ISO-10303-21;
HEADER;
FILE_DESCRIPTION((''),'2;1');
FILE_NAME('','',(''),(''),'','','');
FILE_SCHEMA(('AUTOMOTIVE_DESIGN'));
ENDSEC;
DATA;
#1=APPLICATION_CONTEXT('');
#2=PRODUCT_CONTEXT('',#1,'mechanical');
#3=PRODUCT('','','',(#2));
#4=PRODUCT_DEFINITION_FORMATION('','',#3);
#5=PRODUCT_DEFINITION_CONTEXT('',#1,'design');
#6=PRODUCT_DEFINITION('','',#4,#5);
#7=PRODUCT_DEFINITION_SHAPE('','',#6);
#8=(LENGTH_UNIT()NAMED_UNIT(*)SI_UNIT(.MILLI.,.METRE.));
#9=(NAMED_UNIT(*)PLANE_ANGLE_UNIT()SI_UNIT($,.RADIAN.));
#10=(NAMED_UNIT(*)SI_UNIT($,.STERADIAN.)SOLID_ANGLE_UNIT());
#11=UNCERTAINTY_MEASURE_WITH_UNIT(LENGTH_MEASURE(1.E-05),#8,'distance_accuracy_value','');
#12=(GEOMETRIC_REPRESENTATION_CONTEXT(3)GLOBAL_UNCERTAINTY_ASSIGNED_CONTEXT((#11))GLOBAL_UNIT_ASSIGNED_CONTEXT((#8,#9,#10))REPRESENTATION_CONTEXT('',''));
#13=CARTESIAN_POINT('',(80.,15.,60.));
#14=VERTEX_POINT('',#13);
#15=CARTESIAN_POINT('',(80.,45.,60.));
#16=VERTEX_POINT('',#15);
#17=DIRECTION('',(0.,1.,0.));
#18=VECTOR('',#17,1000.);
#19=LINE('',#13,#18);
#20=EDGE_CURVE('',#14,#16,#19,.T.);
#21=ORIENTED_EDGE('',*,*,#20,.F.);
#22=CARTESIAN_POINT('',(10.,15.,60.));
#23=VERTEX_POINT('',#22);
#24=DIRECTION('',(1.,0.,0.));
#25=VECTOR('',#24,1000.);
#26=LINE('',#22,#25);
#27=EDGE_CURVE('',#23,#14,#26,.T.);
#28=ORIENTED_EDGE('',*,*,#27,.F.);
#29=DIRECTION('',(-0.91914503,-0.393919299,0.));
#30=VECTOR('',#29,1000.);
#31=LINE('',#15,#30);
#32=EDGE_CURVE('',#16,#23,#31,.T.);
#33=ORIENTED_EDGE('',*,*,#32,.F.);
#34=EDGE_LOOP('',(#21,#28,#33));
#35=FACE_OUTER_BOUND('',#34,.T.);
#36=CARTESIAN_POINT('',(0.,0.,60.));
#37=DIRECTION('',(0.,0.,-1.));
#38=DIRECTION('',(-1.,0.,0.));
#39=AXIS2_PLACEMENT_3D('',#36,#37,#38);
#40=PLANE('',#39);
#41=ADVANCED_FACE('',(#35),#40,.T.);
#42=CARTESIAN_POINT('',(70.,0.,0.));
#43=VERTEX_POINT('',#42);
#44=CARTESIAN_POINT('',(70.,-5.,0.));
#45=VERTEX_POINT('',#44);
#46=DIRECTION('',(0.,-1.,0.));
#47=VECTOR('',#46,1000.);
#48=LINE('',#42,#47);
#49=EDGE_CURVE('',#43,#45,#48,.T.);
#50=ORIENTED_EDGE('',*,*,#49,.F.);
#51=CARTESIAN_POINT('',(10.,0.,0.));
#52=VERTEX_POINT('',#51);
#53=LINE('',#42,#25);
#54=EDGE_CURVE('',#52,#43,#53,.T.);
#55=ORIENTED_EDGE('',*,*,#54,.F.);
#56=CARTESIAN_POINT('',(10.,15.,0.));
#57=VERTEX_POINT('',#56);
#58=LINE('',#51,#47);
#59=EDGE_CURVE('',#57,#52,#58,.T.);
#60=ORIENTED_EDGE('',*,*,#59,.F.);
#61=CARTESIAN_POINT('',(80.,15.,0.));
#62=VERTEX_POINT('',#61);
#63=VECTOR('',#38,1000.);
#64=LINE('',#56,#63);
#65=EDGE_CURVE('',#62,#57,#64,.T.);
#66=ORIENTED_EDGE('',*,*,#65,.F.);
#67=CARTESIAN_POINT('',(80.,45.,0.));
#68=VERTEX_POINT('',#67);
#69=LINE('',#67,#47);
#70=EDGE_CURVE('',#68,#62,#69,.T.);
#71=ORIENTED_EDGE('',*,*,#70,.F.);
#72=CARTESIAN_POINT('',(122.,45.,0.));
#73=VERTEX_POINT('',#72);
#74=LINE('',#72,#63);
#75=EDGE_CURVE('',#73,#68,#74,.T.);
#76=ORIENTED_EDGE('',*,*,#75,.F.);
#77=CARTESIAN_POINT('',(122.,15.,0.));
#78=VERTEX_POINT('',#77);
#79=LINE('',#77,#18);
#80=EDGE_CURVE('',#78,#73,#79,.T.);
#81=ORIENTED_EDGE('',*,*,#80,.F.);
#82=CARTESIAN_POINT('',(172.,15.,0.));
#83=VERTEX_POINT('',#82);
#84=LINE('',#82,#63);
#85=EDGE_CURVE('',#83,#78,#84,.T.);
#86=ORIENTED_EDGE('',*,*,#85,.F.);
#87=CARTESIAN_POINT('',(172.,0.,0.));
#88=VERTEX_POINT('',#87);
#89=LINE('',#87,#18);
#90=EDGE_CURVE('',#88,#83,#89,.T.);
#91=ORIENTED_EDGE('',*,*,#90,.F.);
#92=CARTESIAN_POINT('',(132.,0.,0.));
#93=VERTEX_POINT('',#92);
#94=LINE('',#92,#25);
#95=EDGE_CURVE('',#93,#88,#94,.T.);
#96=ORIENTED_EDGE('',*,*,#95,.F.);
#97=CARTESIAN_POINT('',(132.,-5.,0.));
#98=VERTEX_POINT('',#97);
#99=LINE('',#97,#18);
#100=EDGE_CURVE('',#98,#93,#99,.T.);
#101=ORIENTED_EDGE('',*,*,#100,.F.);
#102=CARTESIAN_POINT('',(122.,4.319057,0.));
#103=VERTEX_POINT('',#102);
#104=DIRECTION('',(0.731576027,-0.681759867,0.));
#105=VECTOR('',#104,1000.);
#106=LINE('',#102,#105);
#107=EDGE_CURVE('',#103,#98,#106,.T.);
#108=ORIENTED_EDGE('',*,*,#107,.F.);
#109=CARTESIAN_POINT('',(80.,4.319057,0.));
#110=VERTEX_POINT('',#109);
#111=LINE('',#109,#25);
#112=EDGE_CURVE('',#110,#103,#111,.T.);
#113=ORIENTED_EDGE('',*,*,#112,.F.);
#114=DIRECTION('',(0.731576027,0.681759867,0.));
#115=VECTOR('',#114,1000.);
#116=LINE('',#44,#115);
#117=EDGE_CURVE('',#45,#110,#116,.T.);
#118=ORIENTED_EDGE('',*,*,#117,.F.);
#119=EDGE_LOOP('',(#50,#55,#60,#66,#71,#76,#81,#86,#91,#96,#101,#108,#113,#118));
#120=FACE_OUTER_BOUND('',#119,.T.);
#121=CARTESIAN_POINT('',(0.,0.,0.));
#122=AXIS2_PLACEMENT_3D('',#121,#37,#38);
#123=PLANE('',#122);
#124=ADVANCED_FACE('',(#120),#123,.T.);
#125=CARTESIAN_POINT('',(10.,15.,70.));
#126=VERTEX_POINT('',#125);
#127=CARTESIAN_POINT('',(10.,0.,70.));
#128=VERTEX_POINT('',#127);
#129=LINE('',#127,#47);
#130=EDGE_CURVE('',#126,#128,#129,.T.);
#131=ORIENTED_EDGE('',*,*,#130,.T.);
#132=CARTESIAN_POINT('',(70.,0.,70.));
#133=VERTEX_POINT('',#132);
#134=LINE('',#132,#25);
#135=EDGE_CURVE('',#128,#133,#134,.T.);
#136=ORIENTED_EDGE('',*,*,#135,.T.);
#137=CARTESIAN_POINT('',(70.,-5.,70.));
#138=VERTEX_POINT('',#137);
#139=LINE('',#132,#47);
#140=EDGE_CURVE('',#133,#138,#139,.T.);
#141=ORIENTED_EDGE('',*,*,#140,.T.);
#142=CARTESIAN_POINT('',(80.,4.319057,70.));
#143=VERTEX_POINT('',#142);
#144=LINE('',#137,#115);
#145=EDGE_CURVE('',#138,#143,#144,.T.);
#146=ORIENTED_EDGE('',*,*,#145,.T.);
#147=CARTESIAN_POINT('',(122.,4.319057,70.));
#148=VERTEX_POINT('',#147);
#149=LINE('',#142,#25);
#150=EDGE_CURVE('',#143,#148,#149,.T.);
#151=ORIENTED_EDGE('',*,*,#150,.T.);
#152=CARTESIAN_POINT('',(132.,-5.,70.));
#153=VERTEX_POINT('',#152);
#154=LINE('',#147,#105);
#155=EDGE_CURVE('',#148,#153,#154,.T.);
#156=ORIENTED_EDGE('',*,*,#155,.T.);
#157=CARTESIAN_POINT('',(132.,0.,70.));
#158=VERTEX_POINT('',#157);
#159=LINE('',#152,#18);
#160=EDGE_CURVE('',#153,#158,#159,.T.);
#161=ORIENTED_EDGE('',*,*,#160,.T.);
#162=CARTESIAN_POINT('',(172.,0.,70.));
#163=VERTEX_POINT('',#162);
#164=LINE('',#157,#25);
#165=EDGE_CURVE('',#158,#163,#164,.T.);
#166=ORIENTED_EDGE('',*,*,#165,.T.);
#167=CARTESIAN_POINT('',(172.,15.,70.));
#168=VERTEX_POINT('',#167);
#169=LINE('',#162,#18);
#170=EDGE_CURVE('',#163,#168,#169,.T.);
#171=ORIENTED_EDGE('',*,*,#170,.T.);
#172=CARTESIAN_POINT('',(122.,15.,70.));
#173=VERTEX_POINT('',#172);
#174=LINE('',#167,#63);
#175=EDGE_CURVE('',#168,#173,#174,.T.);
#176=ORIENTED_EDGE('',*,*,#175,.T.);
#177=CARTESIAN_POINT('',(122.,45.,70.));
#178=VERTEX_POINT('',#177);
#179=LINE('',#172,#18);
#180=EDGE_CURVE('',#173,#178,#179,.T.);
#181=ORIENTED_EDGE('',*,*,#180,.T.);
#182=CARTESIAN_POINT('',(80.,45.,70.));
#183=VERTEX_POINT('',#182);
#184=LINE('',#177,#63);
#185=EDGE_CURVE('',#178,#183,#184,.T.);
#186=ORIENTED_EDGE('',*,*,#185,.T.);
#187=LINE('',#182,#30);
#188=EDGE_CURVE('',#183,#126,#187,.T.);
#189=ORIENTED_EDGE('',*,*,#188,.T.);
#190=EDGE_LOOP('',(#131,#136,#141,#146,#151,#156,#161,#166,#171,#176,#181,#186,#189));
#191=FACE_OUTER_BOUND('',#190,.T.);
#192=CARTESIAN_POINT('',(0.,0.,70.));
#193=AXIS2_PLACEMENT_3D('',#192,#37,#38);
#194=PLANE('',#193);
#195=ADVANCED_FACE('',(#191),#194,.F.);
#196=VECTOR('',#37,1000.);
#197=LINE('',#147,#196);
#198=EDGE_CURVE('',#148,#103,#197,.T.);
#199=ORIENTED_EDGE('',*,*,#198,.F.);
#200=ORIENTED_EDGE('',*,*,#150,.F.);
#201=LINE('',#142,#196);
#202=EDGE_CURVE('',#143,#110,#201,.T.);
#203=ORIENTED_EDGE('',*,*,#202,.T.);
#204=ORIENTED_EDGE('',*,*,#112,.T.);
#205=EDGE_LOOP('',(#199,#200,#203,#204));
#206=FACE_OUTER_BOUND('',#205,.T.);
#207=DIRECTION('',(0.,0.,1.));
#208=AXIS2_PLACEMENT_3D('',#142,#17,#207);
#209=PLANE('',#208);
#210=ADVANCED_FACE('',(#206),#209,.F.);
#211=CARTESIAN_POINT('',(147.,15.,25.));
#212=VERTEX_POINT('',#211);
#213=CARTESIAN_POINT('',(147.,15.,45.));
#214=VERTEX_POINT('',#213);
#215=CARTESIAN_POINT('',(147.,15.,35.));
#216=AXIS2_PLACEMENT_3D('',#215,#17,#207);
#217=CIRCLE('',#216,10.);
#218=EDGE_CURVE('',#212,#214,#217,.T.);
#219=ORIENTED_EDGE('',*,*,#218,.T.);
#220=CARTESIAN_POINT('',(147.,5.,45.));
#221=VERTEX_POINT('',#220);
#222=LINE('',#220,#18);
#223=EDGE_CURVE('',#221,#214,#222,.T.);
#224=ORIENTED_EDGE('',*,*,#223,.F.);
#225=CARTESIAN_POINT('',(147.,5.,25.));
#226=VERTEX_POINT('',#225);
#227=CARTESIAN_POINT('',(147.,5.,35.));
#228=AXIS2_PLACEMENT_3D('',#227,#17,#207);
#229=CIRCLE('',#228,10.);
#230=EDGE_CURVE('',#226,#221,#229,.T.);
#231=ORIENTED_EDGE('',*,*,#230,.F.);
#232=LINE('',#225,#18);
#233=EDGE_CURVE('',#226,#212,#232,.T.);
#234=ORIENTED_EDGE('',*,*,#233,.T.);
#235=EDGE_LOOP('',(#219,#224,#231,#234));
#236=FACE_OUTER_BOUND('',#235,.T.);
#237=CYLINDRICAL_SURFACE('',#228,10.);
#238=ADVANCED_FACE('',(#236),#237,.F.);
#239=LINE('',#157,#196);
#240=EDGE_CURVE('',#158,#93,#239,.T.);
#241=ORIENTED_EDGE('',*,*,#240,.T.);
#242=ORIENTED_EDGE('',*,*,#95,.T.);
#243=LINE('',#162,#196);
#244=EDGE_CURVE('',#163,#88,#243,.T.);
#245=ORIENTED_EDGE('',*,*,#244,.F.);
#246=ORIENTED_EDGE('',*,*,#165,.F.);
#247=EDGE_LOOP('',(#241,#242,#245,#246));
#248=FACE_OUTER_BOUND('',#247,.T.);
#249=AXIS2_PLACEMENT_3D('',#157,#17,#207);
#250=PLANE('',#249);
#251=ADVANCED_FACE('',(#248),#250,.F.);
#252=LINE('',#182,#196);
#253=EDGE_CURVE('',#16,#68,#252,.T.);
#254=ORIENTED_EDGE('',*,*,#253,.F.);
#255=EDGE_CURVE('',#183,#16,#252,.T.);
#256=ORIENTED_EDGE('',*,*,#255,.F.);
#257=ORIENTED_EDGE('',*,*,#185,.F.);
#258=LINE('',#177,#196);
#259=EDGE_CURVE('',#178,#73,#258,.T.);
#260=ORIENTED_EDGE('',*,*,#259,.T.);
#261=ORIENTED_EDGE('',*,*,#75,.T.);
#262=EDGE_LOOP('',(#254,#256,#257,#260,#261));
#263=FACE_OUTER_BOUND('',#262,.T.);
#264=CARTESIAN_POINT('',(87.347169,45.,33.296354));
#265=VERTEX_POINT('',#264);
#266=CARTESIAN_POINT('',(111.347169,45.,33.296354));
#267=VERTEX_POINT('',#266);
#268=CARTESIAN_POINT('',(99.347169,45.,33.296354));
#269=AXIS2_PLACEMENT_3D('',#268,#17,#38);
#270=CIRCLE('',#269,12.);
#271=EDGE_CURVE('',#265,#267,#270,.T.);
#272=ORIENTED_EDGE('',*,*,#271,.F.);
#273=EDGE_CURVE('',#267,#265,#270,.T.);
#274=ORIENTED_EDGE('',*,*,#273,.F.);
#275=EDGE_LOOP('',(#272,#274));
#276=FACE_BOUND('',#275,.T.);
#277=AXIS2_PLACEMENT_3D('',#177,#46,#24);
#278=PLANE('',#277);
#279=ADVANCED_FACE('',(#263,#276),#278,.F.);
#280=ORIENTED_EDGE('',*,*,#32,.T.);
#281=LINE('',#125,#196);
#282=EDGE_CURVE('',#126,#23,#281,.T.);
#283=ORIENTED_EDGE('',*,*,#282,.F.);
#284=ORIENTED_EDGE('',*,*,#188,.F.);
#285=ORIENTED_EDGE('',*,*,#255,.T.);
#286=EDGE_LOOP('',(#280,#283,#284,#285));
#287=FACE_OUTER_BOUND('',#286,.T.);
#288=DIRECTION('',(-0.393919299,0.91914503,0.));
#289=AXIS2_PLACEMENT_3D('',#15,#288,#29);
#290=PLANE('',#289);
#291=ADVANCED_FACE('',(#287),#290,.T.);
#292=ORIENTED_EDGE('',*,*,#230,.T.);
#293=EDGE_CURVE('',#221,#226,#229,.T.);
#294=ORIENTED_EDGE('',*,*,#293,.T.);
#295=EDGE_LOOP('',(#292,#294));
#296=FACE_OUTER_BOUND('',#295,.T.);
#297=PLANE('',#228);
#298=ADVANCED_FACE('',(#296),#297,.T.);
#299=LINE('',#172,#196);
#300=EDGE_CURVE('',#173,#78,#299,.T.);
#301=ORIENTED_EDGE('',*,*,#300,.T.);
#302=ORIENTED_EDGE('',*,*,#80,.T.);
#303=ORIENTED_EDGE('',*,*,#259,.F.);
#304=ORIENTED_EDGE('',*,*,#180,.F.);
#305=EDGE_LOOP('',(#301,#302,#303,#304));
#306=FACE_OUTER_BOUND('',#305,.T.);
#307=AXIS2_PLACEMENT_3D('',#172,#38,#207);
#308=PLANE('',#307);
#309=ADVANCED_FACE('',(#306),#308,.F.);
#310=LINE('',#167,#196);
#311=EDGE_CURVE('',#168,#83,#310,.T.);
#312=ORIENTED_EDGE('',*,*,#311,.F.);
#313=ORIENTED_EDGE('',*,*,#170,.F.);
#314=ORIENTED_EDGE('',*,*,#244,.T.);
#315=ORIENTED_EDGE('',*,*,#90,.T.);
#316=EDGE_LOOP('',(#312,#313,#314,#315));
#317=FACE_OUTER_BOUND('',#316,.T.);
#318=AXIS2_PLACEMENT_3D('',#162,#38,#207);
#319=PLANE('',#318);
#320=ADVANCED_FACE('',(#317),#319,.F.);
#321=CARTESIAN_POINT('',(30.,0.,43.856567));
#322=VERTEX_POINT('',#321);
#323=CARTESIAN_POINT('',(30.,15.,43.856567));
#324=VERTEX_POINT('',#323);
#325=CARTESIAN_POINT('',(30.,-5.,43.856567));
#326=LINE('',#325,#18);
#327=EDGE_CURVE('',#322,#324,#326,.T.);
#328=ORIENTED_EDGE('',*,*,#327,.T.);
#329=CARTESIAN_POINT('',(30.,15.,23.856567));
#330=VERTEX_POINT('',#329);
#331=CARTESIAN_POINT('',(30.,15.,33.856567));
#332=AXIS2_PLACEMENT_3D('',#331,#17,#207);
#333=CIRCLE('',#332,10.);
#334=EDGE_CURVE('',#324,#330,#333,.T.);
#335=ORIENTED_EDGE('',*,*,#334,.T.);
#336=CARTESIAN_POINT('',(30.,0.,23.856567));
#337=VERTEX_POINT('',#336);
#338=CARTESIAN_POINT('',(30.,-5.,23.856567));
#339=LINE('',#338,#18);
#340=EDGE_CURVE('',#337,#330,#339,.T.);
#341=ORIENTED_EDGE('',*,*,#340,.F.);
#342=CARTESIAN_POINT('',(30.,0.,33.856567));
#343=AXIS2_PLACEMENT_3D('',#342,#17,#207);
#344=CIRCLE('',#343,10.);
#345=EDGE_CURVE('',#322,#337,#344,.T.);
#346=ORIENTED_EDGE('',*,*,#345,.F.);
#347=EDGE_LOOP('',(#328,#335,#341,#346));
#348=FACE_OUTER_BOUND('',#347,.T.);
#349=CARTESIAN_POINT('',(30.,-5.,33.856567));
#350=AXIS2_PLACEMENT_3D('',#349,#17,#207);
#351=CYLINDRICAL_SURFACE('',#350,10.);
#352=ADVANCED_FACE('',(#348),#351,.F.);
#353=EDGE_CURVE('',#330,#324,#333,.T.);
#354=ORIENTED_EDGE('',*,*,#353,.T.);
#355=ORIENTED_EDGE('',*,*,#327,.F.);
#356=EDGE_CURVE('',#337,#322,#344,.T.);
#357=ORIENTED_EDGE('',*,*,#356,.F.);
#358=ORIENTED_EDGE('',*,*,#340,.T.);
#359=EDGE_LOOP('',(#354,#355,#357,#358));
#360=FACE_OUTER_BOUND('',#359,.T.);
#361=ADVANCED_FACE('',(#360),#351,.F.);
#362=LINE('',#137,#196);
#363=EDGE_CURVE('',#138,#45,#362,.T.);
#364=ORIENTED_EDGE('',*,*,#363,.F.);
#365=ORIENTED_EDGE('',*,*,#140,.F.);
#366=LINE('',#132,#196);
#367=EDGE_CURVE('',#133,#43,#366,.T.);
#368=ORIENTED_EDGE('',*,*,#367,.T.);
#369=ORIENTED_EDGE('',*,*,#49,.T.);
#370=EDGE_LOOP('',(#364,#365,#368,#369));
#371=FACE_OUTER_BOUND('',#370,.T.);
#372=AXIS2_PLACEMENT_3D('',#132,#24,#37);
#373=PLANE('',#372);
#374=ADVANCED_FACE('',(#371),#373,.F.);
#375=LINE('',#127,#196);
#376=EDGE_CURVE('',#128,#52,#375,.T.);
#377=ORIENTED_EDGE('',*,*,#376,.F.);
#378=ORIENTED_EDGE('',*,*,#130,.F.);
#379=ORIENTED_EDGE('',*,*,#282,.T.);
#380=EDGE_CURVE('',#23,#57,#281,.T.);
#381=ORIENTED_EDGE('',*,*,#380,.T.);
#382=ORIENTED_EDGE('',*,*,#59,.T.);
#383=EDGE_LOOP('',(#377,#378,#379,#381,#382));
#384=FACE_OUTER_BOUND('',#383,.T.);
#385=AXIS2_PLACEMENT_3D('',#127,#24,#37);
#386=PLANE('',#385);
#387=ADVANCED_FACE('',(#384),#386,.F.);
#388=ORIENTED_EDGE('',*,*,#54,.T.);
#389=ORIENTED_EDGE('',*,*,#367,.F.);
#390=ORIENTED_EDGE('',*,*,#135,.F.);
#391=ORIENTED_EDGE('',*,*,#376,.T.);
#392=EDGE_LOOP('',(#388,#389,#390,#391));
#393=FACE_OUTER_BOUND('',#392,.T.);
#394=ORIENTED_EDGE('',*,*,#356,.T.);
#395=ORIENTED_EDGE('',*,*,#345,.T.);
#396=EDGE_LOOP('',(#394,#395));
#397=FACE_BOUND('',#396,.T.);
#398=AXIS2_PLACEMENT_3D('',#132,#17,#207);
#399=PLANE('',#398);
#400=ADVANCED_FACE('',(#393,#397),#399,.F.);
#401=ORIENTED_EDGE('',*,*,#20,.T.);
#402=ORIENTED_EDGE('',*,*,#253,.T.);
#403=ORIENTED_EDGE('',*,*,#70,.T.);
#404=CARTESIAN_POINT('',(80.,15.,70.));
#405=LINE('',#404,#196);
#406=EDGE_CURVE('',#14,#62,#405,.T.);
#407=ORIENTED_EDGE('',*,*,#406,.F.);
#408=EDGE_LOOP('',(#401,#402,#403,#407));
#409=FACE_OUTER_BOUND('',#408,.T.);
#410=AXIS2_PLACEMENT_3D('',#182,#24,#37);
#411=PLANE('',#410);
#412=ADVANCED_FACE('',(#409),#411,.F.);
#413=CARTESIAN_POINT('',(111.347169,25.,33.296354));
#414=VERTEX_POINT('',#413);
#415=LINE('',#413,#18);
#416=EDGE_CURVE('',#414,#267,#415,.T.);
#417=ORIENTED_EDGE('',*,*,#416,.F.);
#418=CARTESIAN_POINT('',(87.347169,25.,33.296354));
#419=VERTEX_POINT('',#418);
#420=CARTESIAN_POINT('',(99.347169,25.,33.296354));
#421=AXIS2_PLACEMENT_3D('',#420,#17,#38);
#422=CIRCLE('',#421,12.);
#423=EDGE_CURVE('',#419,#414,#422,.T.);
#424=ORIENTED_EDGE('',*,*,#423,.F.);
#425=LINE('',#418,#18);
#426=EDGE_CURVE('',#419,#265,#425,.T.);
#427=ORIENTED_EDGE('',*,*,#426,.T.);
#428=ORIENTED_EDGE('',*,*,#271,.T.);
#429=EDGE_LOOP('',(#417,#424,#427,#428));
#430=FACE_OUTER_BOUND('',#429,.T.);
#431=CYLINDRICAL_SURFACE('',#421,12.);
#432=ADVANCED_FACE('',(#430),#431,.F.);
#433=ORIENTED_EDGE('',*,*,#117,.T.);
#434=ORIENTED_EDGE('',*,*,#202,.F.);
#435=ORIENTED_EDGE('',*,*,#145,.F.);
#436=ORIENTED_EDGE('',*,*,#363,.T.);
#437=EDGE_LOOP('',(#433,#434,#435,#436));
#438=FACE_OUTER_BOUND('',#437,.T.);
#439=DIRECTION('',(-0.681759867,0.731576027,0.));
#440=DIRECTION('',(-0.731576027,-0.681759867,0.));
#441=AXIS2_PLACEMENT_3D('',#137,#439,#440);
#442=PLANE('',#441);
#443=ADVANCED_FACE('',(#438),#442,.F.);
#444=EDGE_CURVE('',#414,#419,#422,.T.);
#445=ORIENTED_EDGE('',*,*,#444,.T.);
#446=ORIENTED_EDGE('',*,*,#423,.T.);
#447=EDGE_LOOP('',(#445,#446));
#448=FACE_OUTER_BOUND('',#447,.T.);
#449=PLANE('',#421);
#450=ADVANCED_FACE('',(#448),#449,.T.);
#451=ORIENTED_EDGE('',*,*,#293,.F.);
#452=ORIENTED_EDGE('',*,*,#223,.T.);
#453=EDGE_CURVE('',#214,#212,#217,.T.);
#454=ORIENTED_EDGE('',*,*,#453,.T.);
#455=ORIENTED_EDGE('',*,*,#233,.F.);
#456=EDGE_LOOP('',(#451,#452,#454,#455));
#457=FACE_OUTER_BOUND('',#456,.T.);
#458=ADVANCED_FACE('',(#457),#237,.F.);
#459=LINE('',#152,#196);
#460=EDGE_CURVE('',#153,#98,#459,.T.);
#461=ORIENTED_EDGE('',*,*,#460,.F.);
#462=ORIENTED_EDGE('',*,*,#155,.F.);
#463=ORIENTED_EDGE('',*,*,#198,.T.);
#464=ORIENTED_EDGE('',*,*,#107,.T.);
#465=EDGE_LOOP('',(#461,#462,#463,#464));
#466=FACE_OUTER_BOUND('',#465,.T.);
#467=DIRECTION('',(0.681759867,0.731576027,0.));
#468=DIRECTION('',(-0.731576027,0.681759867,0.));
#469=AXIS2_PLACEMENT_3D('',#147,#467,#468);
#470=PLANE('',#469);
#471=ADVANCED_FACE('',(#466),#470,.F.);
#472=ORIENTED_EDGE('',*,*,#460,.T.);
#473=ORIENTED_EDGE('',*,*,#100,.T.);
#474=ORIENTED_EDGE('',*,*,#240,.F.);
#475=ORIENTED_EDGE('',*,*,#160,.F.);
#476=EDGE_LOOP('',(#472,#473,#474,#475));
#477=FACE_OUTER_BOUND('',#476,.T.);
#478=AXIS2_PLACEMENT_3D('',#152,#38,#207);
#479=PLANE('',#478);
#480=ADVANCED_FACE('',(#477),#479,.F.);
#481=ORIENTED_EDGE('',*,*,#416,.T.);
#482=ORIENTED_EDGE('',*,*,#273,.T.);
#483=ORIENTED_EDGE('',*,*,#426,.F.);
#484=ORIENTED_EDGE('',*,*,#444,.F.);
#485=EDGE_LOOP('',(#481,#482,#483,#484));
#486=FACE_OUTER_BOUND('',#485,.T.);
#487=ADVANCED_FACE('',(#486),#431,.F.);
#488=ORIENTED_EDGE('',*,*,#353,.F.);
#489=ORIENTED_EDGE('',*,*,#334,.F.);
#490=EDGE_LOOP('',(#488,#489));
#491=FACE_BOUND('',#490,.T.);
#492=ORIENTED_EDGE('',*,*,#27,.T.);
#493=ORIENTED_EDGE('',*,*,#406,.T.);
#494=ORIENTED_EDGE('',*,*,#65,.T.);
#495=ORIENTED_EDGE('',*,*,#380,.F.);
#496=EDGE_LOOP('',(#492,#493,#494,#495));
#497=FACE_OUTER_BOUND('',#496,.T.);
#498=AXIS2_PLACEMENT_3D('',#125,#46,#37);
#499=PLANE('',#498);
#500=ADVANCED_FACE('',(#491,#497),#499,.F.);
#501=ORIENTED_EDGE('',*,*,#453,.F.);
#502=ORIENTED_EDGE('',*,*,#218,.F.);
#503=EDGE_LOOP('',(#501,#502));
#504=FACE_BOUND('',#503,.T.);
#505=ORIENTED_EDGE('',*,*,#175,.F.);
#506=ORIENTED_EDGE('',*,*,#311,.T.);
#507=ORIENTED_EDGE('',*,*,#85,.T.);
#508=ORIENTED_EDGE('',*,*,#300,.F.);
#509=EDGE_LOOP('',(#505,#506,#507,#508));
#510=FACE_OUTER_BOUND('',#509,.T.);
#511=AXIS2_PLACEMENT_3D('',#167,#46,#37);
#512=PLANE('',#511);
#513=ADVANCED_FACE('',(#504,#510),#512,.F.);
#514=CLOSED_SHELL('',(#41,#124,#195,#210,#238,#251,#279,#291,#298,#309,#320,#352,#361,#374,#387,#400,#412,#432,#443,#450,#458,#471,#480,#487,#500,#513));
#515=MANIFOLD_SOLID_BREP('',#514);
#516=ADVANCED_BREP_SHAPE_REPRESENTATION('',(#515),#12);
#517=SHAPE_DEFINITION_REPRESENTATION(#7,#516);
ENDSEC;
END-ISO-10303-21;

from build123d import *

# Parameters (mm, degrees)
STEPPED_BLOCK_BODY_DEPTH = 70
HOLE_A_SKETCH_R          = 10
HOLE_A_DEPTH_20_DEPTH    = 20
HOLE_B_SKETCH_R          = 12
HOLE_B_DEPTH_20_DEPTH    = 20
TRIANGULAR_LUG_DEPTH     = 10
ROUND_BOSS_SKETCH_R      = 10
ROUND_BOSS_10MM_DEPTH    = 10
HOLE_C_SKETCH_R          = 10
HOLE_C_DEPTH_10_DEPTH    = 10


with BuildPart() as part:
    # Stepped Block Profile Sketch → Stepped Block Body (new body)
    with BuildSketch(Plane.XY):
        Polygon((70, 0), (70, -5), (80, 4.319056963), (122, 4.319056963), (132, -5), (132, 0), (172, 0), (172, 15), (122, 15), (122, 45), (80, 45), (80, 15), (10, 15), (10, 0), align=None)
    extrude(amount=STEPPED_BLOCK_BODY_DEPTH)

    # Hole A Sketch → Hole A Depth 20 (cut)
    with BuildSketch(Plane(origin=(0, 15, 0), x_dir=(1, 0, 0), z_dir=(0, 1, 0))):
        with Locations(Location((30, -33.856567252, 0), (0, 0, 270))):
            Circle(HOLE_A_SKETCH_R)
    extrude(amount=-HOLE_A_DEPTH_20_DEPTH, mode=Mode.SUBTRACT)

    # Hole B Sketch → Hole B Depth 20 (cut)
    with BuildSketch(Plane(origin=(0, 45, 0), x_dir=(1, 0, 0), z_dir=(0, 1, 0))):
        with Locations(Location((99.347169036, -33.296354443, 0), (0, 0, 180))):
            Circle(HOLE_B_SKETCH_R)
    extrude(amount=-HOLE_B_DEPTH_20_DEPTH, mode=Mode.SUBTRACT)

    # Triangular Lug Sketch → Triangular Lug (add)
    with BuildSketch(Plane.XY.offset(70)):
        Polygon((10, 15), (80, 15), (80, 45), align=None)
    extrude(amount=-TRIANGULAR_LUG_DEPTH)

    # Round Boss Sketch → Round Boss 10mm (add)
    with BuildSketch(Plane(origin=(0, 15, 0), x_dir=(1, 0, 0), z_dir=(0, 1, 0))):
        with Locations((147.541656159, -38.188385292)):
            Circle(ROUND_BOSS_SKETCH_R)
    extrude(amount=-ROUND_BOSS_10MM_DEPTH)

    # Hole C Sketch → Hole C Depth 10 (cut)
    with BuildSketch(Plane(origin=(0, 15, 0), x_dir=(1, 0, 0), z_dir=(0, 1, 0))):
        with Locations(Location((147, -35, 0), (0, 0, 270))):
            Circle(HOLE_C_SKETCH_R)
    extrude(amount=-HOLE_C_DEPTH_10_DEPTH, mode=Mode.SUBTRACT)


solid = part.part
